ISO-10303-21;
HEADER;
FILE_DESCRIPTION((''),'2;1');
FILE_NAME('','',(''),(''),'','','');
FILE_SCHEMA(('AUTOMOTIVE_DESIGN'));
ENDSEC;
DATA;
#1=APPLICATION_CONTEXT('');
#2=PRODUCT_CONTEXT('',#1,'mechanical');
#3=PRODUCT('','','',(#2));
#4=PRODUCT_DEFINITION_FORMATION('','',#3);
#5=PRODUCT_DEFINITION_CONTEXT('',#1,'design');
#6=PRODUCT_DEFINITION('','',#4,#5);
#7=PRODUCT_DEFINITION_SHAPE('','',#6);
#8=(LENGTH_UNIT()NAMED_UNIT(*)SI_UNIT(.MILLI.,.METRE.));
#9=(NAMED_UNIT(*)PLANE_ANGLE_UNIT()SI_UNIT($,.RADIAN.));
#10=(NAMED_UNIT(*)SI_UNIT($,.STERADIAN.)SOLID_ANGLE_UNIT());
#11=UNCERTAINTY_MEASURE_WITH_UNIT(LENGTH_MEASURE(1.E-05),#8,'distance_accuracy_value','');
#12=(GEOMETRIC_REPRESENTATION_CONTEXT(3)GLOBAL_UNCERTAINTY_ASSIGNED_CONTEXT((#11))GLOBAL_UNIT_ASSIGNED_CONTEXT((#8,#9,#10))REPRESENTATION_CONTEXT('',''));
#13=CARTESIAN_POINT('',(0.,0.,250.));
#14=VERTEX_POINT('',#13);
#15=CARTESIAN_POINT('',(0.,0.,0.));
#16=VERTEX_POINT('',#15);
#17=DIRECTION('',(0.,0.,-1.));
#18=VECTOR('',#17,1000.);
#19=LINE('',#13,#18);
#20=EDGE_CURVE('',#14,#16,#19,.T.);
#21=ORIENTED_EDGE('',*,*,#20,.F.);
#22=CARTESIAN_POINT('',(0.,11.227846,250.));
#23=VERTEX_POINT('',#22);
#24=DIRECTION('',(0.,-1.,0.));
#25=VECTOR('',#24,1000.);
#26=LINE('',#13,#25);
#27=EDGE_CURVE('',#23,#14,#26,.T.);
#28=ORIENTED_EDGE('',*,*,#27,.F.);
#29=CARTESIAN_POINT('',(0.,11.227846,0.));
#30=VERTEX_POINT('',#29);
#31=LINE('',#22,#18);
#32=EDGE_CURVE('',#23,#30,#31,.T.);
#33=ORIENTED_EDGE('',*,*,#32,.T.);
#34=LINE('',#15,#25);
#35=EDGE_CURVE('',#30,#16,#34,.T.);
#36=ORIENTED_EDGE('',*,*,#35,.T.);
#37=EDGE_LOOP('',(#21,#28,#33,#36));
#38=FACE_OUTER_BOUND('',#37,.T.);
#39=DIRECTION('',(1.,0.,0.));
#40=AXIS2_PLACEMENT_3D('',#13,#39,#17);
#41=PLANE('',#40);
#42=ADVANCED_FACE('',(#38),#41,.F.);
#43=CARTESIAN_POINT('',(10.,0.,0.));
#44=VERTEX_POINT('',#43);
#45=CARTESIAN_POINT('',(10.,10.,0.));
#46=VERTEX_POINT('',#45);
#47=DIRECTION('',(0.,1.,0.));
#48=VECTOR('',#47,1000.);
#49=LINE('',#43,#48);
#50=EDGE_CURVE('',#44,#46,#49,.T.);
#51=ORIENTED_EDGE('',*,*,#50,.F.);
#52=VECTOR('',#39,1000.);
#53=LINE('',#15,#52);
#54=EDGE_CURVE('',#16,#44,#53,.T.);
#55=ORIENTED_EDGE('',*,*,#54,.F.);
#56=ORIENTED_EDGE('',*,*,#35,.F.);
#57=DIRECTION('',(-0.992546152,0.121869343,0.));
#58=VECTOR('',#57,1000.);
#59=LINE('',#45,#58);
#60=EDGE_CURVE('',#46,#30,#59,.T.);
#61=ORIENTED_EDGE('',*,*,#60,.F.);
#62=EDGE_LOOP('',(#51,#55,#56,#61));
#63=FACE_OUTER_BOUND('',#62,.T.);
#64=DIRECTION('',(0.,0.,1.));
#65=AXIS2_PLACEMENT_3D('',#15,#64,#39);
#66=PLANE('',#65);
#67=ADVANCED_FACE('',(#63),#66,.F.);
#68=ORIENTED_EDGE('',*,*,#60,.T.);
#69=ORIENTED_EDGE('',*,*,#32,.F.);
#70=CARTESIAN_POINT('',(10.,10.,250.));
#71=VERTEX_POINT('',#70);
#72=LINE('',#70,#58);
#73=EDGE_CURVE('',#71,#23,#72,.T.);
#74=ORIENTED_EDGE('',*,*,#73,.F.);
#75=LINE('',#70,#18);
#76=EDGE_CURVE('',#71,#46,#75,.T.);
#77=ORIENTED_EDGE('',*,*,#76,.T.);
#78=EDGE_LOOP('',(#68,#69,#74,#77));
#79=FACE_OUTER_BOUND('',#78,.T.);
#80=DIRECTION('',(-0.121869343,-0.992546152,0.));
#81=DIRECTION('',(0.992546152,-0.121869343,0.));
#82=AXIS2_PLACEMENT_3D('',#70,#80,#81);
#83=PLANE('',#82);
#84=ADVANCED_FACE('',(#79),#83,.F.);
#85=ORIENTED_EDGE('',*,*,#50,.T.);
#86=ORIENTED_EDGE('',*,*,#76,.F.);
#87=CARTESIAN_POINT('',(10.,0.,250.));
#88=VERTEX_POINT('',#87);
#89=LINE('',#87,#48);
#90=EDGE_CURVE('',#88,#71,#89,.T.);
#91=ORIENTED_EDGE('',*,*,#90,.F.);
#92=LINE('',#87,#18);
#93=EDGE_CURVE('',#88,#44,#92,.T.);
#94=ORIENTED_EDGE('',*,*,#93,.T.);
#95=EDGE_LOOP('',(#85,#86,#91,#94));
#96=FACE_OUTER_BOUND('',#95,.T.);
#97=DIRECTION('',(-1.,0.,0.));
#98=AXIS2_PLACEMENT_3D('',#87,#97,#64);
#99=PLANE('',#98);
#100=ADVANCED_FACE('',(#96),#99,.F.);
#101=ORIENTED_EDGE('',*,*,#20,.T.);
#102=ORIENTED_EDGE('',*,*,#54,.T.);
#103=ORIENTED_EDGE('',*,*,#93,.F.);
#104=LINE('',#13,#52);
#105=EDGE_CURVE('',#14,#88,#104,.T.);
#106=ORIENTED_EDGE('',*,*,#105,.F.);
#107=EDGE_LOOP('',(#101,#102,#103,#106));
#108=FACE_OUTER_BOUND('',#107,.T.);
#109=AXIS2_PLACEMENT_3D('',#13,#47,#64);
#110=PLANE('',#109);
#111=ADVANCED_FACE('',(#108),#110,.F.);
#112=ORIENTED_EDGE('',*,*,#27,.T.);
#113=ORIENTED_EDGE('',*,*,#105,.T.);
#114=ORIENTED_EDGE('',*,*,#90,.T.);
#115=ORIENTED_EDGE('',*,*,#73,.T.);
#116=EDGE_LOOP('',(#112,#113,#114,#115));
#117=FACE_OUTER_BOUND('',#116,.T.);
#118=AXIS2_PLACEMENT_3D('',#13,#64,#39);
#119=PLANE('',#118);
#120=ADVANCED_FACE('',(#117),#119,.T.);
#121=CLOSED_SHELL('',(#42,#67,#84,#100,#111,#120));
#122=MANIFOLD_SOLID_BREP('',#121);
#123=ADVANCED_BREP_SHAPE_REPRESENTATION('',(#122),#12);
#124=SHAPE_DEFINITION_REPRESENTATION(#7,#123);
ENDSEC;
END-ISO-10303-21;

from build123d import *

# Parameters (mm, degrees)
BOSS_EXTRUDE1_DEPTH = 250


with BuildPart() as part:
    # Sketch1 → Boss-Extrude1 (new body)
    with BuildSketch(Plane.XY):
        Polygon((0, 0), (0, 11.227845609), (10, 10), (10, 0), align=None)
    extrude(amount=BOSS_EXTRUDE1_DEPTH)


solid = part.part
